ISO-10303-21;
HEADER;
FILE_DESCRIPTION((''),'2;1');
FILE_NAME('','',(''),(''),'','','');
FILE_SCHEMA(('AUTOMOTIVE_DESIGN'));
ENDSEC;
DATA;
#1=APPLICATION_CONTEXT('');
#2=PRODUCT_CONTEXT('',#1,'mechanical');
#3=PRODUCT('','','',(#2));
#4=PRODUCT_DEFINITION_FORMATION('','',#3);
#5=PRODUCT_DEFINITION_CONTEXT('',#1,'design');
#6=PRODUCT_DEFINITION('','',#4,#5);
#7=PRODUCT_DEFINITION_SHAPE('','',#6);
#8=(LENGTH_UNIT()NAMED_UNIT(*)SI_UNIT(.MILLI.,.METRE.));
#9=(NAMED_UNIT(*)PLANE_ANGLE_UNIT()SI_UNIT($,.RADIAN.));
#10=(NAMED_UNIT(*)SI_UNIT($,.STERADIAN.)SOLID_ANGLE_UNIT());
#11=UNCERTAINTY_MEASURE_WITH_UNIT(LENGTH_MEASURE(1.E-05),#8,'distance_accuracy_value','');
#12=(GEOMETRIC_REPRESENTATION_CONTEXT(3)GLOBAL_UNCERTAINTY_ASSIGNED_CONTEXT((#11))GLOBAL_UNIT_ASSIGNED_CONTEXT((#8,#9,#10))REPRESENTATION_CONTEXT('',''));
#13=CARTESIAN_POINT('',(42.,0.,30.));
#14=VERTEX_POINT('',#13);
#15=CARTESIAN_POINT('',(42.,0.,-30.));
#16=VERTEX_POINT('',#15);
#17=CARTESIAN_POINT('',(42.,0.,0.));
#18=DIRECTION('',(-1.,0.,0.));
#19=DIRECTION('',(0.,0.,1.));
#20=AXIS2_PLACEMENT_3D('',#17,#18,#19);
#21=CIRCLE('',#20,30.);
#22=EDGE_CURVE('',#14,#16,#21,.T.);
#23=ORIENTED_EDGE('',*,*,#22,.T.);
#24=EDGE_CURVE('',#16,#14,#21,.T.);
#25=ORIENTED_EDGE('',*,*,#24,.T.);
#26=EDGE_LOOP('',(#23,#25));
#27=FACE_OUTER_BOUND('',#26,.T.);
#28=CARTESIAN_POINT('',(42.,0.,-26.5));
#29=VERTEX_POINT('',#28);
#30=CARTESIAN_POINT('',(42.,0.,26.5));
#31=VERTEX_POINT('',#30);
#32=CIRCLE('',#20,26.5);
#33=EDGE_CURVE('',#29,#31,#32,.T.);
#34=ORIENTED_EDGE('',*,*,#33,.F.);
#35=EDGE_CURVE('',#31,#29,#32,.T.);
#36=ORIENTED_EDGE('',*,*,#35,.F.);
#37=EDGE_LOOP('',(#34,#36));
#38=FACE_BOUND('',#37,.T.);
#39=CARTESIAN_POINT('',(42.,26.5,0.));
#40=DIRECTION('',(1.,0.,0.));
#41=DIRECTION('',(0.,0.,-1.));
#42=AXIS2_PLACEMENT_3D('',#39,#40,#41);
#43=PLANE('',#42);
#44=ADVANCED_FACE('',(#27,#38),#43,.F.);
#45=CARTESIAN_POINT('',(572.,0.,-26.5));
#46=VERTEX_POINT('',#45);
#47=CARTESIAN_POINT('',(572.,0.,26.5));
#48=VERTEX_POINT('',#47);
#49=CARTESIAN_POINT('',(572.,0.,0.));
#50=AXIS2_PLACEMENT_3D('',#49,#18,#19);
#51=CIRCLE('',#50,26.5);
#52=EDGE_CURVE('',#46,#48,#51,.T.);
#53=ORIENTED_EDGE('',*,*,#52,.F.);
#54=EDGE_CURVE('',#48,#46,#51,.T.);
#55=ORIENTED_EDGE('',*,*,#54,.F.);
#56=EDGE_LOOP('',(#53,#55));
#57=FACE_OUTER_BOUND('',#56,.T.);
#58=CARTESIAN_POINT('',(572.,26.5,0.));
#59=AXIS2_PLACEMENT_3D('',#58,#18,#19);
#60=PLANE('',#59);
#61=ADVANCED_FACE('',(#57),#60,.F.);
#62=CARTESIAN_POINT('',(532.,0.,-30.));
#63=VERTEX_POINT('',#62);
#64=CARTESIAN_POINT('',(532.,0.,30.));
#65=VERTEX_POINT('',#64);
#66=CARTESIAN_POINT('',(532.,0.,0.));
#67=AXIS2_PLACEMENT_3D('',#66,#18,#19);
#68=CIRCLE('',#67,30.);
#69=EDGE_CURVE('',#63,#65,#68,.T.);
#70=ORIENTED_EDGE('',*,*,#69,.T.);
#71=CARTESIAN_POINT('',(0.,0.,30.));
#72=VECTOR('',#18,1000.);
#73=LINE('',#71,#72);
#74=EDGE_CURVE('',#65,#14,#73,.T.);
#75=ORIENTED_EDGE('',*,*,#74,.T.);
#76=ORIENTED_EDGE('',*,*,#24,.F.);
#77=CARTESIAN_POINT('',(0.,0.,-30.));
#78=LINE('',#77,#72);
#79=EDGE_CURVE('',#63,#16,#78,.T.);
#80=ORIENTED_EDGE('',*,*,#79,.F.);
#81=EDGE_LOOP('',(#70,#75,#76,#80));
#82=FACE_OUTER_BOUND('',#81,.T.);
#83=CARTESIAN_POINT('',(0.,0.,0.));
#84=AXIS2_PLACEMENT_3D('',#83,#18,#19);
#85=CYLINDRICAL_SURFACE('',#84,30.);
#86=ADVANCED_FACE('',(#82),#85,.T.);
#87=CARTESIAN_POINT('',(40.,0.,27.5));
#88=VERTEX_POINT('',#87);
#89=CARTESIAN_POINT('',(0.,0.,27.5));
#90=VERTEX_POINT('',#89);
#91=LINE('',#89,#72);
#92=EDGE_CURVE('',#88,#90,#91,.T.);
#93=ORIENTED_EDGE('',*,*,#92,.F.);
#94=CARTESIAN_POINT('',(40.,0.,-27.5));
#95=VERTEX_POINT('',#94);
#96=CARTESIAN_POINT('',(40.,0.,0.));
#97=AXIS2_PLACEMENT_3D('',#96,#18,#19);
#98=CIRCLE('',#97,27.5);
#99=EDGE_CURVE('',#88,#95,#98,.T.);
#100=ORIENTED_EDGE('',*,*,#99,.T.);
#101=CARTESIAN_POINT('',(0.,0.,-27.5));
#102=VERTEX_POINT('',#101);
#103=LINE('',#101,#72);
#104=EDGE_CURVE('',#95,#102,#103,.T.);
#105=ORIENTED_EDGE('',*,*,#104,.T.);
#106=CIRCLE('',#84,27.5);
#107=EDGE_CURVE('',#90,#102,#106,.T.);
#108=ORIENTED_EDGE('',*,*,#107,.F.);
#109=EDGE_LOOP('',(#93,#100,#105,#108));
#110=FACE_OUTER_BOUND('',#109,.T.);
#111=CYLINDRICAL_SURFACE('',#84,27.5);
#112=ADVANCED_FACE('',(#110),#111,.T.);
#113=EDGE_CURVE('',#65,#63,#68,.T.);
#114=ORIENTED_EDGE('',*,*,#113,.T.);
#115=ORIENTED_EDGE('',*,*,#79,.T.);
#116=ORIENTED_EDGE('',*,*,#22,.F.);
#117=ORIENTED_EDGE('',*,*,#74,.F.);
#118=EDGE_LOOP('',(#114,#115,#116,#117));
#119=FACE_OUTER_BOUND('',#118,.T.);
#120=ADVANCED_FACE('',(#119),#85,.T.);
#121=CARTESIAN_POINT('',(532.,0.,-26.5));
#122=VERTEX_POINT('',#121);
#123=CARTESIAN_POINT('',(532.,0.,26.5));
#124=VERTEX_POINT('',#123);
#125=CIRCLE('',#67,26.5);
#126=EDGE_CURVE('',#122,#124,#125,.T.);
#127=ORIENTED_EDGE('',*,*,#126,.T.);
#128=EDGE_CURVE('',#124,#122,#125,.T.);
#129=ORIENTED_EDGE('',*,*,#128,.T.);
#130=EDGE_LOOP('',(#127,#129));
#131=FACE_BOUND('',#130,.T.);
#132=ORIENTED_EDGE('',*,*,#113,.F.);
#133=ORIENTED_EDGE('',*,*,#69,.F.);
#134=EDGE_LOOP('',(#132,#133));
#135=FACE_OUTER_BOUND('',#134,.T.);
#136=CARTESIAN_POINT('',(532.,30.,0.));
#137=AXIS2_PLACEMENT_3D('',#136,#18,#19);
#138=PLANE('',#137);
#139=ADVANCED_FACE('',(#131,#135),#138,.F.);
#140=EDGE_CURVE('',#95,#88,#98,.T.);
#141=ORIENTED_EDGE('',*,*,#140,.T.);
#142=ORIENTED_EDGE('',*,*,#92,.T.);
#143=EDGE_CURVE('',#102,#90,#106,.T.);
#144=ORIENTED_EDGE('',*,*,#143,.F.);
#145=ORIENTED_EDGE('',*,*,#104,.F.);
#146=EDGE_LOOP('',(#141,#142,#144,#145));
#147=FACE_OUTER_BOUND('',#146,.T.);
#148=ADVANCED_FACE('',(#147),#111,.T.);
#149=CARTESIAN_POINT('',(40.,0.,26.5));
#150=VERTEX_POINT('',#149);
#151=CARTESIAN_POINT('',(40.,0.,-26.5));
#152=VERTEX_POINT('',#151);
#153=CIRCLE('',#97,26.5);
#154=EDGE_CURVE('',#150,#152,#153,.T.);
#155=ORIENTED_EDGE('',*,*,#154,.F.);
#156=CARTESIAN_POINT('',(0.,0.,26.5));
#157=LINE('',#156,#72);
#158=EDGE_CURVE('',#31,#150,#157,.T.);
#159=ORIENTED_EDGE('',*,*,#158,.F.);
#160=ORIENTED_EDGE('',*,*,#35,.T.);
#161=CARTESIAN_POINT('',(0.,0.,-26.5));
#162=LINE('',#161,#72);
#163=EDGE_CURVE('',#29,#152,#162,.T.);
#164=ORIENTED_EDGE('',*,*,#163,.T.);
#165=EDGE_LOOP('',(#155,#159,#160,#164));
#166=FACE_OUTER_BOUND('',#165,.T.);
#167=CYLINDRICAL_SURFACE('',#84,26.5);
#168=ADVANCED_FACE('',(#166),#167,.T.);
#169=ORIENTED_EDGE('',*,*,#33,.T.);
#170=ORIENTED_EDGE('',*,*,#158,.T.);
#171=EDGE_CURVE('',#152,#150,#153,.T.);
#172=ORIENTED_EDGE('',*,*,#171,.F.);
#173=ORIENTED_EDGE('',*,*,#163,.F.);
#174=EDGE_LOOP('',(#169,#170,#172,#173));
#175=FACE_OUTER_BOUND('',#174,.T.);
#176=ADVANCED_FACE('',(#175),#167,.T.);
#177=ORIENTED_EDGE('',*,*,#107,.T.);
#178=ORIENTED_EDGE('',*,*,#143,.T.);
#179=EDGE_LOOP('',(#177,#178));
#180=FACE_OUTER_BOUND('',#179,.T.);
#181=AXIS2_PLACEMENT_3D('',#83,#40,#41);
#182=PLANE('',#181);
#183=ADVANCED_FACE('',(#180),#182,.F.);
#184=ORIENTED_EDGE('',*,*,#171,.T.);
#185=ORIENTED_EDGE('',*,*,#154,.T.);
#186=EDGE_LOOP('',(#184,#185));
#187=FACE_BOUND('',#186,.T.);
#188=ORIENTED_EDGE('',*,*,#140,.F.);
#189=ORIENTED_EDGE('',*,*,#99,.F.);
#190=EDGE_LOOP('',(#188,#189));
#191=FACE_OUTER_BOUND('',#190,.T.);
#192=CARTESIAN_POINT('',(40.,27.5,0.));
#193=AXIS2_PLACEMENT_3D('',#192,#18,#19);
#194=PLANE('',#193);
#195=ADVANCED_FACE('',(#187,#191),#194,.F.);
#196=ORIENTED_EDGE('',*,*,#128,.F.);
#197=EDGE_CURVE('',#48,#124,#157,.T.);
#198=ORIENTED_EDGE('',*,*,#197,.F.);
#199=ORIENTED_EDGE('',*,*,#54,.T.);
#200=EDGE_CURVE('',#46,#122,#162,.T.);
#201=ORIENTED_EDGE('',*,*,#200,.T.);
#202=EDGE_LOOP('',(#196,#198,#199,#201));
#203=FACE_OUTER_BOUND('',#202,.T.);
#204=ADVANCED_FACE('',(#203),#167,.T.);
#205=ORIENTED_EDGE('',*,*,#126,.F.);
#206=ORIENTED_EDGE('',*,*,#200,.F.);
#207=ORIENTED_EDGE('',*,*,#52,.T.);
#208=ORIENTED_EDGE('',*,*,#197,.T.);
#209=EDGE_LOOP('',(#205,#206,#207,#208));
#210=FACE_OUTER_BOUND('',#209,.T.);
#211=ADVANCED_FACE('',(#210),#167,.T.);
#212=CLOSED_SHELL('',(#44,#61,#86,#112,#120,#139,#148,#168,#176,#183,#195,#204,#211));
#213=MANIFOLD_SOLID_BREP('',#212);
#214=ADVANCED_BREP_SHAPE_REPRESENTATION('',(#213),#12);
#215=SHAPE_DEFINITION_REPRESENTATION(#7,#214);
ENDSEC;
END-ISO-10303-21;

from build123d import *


with BuildPart() as part:
    # 草图1 → 旋转1 (revolve)
    with BuildSketch(Plane.XY, mode=Mode.PRIVATE) as revolve_1_sk:
        Polygon((0, 0), (0, 27.5), (40, 27.5), (40, 26.5), (42, 26.5), (42, 30), (532, 30), (532, 26.5), (572, 26.5), (572, 0), align=None)
    revolve(revolve_1_sk.sketch.rotate(Axis((0, 0, 0), (1, 0, 0)), 90), axis=Axis((0, 0, 0), (1, 0, 0)))


solid = part.part
